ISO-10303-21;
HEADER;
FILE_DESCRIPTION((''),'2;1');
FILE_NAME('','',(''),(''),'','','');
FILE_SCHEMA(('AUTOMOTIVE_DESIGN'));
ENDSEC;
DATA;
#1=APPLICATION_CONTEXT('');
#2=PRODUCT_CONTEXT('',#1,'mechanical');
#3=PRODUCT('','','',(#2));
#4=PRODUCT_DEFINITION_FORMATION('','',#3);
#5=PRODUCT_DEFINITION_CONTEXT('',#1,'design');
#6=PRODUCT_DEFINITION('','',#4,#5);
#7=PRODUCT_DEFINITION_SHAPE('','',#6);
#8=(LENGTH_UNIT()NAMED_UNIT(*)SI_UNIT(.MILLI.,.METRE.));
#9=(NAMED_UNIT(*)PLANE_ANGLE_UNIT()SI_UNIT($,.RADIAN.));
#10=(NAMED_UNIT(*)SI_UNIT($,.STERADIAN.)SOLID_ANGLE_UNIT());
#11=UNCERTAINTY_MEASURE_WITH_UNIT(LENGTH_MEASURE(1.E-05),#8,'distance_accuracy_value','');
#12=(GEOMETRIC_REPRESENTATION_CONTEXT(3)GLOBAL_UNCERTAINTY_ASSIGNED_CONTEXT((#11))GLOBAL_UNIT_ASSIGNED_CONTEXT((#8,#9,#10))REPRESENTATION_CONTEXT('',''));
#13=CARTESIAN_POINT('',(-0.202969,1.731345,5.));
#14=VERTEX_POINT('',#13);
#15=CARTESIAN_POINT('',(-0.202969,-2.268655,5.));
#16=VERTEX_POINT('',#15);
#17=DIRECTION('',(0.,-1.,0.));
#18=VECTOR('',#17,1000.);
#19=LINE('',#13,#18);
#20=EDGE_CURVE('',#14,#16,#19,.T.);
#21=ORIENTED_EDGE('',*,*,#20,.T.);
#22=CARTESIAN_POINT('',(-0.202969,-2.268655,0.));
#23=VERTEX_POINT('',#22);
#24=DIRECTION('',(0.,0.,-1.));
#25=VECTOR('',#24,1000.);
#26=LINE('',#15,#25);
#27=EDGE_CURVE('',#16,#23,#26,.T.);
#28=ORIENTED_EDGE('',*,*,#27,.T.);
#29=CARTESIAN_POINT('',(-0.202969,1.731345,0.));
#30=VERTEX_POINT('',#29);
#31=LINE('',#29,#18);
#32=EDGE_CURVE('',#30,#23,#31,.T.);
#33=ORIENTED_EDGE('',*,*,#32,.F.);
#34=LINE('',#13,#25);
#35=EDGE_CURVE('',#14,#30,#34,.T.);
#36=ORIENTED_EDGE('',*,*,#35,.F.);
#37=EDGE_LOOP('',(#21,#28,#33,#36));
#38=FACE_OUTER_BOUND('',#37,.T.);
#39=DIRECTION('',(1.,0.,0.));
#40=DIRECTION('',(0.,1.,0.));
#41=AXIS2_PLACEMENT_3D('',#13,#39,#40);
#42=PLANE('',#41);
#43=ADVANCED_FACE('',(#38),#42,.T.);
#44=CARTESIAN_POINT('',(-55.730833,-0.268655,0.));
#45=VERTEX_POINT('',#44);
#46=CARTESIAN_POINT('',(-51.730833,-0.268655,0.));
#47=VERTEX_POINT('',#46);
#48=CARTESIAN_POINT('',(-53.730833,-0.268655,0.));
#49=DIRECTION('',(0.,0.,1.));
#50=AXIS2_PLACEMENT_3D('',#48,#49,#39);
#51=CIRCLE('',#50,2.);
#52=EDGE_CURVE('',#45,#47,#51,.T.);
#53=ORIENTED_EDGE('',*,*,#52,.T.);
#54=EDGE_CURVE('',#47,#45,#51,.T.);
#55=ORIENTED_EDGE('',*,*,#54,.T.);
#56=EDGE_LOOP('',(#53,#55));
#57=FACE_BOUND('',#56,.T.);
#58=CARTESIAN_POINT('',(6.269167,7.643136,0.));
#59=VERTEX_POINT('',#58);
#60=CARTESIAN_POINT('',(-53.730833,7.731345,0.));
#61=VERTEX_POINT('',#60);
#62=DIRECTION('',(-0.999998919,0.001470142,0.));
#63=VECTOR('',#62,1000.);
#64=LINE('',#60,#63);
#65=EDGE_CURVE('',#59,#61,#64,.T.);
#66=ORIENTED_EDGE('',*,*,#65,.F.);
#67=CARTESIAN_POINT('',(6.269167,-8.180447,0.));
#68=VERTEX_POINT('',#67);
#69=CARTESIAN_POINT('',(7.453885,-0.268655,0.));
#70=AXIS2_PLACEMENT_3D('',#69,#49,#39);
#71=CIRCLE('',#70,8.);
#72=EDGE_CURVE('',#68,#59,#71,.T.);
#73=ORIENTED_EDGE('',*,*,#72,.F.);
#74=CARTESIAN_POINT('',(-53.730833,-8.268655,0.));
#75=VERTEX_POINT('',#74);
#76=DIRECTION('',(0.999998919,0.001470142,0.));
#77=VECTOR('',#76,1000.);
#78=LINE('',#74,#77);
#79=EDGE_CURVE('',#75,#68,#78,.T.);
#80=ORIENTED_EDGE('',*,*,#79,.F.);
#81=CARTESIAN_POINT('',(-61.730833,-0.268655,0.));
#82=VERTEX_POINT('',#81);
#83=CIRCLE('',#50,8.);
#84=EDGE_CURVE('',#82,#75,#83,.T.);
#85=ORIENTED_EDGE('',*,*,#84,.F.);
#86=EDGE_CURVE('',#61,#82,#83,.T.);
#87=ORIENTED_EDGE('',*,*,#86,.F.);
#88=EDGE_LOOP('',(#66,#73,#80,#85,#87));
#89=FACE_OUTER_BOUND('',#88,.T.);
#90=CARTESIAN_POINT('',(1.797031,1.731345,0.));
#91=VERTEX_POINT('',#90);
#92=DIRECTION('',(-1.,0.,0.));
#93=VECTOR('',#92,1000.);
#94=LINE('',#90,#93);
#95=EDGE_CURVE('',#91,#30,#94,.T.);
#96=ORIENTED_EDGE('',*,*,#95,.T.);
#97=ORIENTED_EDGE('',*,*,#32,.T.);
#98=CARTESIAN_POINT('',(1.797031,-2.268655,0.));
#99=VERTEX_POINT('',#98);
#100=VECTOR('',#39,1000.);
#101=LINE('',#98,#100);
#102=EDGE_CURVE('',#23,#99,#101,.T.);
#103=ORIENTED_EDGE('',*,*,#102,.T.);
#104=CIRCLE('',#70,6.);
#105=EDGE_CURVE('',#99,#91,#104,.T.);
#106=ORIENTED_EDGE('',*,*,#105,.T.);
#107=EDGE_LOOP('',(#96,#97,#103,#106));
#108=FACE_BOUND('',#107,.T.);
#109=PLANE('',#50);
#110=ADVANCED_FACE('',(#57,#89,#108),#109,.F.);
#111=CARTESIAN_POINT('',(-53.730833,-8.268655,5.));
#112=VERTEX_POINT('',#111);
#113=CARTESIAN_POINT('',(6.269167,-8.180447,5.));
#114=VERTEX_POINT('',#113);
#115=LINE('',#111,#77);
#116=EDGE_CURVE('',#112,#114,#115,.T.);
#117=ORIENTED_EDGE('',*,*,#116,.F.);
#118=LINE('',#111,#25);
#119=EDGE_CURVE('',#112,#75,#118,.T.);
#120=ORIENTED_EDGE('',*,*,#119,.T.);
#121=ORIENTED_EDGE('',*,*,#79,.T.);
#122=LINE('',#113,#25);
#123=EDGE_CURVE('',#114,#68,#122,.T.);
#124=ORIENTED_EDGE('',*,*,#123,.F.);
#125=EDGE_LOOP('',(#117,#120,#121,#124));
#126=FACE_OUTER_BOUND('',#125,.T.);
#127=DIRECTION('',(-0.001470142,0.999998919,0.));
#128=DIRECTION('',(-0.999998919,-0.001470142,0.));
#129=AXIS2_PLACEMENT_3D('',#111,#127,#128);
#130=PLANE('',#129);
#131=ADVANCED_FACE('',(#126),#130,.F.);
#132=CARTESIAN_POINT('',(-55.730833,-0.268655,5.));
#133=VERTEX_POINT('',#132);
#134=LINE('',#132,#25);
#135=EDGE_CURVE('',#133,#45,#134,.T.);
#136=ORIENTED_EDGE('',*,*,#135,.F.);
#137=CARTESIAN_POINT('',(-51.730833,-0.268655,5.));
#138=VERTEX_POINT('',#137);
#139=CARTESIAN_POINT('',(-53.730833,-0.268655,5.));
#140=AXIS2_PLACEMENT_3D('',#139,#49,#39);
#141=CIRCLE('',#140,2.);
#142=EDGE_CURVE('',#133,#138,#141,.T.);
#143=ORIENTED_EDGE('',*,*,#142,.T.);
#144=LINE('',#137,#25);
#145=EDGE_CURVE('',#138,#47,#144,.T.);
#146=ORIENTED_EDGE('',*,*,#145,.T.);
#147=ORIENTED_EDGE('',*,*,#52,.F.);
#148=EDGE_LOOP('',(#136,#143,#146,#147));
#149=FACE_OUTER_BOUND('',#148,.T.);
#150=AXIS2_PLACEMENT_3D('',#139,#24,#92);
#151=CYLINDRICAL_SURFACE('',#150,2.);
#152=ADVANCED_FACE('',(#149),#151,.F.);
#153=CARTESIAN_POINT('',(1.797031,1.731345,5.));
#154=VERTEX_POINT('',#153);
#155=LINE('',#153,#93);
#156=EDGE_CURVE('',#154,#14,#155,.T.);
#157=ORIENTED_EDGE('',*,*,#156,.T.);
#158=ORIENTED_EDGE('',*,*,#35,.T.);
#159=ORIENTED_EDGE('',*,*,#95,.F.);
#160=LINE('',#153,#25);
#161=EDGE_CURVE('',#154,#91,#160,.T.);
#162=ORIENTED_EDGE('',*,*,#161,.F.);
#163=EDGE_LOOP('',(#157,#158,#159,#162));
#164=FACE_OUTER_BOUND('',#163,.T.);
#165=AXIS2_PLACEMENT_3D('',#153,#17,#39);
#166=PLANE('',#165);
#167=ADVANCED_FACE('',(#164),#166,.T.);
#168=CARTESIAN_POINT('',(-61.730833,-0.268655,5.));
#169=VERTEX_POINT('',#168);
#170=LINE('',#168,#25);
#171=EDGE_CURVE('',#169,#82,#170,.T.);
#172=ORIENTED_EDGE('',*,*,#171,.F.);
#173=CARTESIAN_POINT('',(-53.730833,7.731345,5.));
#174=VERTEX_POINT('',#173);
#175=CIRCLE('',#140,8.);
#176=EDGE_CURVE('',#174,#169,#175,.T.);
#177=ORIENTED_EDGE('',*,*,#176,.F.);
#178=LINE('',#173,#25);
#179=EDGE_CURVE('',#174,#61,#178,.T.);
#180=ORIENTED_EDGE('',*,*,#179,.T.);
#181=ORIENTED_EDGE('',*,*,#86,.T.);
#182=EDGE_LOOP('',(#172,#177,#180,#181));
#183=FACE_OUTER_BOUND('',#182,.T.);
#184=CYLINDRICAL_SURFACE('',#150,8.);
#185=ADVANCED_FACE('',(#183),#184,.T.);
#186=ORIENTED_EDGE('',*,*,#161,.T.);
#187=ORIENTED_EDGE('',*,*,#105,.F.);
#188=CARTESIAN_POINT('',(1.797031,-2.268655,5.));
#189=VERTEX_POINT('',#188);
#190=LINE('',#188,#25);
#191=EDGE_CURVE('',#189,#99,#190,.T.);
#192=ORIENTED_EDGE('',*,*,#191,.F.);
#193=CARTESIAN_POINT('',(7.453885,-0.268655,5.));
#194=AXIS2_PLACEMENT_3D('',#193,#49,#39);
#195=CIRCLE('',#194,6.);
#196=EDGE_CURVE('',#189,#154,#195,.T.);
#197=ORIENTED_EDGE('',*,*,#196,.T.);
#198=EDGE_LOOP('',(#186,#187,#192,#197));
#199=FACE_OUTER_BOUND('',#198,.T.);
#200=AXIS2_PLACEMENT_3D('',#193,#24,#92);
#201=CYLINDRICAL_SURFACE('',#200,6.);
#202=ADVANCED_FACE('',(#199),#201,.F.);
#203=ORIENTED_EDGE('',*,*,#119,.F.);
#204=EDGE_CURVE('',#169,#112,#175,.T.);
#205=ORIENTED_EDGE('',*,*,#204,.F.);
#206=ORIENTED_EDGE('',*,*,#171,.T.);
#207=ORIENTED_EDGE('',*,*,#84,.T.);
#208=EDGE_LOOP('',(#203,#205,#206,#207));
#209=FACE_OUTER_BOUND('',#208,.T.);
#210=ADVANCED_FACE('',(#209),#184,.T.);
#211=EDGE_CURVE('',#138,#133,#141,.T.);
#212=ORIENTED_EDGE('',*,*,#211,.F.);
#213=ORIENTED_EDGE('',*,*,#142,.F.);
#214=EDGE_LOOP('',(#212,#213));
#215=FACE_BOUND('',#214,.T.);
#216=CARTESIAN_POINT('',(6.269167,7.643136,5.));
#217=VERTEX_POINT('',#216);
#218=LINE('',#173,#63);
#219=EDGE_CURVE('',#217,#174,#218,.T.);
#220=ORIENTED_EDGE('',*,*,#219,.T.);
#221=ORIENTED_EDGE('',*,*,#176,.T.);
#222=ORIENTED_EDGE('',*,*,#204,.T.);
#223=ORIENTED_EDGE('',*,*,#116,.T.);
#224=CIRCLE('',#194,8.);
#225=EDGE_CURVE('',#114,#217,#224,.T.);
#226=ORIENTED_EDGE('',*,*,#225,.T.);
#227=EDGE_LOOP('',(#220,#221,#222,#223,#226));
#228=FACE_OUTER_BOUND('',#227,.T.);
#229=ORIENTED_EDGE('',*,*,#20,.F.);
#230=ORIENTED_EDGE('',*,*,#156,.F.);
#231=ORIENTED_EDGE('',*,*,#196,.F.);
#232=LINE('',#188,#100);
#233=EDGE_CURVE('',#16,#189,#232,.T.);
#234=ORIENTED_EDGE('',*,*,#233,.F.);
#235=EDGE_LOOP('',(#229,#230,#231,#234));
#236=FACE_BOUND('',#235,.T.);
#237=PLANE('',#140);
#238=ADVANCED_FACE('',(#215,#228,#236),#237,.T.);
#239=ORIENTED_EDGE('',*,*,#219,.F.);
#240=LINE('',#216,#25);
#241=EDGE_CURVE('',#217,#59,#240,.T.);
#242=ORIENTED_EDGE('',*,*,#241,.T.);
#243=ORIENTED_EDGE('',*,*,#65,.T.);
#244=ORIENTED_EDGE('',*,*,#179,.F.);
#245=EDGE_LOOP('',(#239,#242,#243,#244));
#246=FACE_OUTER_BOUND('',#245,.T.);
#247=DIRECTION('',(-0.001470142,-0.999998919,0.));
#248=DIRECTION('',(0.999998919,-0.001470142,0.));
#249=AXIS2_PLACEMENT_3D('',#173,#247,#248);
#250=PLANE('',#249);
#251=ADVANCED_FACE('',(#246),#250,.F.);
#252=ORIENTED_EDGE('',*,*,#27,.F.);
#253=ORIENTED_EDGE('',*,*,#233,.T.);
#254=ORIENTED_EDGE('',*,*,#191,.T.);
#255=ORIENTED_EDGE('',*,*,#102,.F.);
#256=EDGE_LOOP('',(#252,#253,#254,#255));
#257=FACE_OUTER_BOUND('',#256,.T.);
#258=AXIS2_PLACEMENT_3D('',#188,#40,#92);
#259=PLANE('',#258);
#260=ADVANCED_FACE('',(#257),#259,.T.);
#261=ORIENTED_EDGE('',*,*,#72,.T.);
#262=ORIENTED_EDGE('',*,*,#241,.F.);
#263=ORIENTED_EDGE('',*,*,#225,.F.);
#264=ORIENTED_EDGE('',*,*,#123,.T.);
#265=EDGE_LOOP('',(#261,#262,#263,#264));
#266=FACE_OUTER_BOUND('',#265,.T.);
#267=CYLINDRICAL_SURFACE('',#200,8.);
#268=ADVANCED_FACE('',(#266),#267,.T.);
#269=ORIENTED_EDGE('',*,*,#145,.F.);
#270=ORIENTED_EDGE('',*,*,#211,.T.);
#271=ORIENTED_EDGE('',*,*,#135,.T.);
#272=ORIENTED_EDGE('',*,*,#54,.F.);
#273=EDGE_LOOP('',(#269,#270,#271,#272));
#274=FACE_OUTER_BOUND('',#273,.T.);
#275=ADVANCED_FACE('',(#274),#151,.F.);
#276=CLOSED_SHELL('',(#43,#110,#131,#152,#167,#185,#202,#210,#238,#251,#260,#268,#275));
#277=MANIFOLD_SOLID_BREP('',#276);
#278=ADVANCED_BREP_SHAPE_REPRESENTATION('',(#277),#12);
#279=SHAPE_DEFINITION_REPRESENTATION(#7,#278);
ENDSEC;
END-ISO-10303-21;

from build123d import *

# Parameters (mm, degrees)
SKETCH_1_R      = 2
EXTRUDE_1_DEPTH = 5


with BuildPart() as part:
    # 草图1 → 凸台-拉伸1 (new body)
    with BuildSketch(Plane.XY):
        with BuildLine():
            Line((-53.730833149, 7.731344519), (6.269166851, 7.643135881))
            ThreePointArc((6.269166851, 7.643135881), (15.453885145, -0.268655481), (6.269166851, -8.180446844))
            Line((6.269166851, -8.180446844), (-53.730833149, -8.268655481))
            ThreePointArc((-53.730833149, -8.268655481), (-61.730833149, -0.268655481), (-53.730833149, 7.731344519))
        make_face()
        with Locations((-53.730833149, -0.268655481)):
            Circle(SKETCH_1_R, mode=Mode.SUBTRACT)
        with BuildLine():
            Line((-0.202969104, 1.731344519), (-0.202969104, -2.268655481))
            Line((-0.202969104, -2.268655481), (1.797030896, -2.268655481))
            ThreePointArc((1.797030896, -2.268655481), (13.453885145, -0.268655481), (1.797030896, 1.731344519))
            Line((1.797030896, 1.731344519), (-0.202969104, 1.731344519))
        make_face(mode=Mode.SUBTRACT)
    extrude(amount=EXTRUDE_1_DEPTH)


solid = part.part
